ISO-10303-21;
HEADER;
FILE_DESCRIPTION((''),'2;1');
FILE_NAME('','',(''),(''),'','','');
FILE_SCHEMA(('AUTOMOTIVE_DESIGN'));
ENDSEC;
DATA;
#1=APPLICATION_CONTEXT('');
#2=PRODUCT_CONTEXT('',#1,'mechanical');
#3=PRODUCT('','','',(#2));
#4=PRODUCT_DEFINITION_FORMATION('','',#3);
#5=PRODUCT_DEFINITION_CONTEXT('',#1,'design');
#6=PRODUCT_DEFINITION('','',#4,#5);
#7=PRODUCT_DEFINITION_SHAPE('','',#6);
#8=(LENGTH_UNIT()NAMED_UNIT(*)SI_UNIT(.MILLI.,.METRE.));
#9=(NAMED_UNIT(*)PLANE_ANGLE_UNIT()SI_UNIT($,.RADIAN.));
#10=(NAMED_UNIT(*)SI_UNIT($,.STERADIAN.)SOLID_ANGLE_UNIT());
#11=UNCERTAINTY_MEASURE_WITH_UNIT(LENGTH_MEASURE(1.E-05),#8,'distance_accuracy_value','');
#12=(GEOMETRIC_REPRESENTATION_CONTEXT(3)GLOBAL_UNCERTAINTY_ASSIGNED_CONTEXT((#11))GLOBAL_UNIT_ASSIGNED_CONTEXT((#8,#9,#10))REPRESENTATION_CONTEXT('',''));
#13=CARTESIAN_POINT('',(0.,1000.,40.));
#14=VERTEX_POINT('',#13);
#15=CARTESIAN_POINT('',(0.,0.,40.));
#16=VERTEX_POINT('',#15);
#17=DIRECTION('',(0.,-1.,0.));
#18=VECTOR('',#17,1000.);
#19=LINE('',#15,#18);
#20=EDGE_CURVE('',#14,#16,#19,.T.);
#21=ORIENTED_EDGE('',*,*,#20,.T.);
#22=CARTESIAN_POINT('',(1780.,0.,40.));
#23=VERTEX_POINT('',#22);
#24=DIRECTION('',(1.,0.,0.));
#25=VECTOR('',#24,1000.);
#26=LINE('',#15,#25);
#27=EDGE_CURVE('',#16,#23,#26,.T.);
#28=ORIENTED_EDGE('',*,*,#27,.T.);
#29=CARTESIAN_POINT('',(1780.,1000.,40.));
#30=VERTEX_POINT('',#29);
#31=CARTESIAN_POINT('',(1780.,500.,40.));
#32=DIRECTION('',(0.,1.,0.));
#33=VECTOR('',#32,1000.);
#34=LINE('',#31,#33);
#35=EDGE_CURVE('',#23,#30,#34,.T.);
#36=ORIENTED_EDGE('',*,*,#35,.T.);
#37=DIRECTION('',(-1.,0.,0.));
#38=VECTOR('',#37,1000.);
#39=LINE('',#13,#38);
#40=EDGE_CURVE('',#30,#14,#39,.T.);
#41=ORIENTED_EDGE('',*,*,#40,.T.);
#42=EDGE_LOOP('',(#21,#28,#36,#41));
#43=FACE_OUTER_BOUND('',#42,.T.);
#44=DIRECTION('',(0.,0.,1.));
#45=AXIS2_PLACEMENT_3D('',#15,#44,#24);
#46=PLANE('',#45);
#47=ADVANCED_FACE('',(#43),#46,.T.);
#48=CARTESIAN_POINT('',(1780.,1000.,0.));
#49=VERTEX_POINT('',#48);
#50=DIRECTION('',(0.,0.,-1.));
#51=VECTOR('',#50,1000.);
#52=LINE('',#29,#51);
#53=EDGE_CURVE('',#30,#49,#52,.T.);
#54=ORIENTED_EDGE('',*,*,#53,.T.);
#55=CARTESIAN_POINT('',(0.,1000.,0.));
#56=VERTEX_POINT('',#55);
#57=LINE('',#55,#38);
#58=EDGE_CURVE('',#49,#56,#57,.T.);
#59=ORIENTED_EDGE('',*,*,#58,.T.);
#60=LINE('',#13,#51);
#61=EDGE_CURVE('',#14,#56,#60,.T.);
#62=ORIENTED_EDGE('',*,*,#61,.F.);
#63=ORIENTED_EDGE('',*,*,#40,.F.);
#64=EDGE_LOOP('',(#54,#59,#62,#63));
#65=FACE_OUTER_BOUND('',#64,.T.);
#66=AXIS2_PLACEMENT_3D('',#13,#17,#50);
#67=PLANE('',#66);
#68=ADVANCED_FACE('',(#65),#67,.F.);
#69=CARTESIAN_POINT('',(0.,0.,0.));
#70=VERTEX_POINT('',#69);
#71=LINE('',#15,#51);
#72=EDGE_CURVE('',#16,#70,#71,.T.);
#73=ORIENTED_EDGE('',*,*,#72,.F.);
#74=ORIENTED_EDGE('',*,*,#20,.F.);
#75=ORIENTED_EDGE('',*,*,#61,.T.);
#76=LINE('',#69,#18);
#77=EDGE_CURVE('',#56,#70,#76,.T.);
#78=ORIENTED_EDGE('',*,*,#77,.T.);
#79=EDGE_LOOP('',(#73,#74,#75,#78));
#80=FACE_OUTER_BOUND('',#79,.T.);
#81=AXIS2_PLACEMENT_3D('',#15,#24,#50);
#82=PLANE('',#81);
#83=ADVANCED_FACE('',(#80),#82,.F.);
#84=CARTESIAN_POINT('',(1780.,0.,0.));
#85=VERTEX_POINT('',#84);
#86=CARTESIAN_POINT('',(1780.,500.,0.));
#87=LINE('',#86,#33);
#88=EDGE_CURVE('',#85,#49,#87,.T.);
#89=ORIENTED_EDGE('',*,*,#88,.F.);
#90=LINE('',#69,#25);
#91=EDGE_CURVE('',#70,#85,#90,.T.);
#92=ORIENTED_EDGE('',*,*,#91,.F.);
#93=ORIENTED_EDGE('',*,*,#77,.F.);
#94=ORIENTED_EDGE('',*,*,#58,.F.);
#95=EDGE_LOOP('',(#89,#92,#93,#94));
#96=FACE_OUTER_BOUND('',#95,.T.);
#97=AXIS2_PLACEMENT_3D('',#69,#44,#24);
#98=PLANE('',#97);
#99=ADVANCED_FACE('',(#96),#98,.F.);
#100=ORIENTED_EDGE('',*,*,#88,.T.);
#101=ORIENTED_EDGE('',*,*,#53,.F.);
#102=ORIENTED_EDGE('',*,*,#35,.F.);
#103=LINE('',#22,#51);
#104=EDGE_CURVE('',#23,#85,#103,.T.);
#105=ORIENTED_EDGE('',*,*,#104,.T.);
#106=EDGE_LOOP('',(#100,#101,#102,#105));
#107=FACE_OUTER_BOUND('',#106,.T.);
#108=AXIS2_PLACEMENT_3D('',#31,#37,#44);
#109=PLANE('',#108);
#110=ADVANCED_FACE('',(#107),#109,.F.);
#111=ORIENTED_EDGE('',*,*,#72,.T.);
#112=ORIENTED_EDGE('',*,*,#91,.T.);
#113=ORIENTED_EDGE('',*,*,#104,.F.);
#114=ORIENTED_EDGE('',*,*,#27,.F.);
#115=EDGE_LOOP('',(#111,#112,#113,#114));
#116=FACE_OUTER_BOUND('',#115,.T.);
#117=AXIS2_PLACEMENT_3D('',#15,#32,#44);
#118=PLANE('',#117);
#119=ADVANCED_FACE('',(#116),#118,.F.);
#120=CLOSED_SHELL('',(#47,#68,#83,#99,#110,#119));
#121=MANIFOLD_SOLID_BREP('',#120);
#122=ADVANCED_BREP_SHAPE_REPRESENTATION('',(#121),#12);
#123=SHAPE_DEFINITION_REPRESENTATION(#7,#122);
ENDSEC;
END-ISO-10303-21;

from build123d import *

# Parameters (mm, degrees)
BOSS_EXTRUDE1_DEPTH = 40


with BuildPart() as part:
    # Sketch1 → Boss-Extrude1 (new body)
    with BuildSketch(Plane.XY):
        Polygon((0, 0), (0, 1000), (1780, 1000), (1780, 500), (1780, 0), align=None)
    extrude(amount=BOSS_EXTRUDE1_DEPTH)


solid = part.part
